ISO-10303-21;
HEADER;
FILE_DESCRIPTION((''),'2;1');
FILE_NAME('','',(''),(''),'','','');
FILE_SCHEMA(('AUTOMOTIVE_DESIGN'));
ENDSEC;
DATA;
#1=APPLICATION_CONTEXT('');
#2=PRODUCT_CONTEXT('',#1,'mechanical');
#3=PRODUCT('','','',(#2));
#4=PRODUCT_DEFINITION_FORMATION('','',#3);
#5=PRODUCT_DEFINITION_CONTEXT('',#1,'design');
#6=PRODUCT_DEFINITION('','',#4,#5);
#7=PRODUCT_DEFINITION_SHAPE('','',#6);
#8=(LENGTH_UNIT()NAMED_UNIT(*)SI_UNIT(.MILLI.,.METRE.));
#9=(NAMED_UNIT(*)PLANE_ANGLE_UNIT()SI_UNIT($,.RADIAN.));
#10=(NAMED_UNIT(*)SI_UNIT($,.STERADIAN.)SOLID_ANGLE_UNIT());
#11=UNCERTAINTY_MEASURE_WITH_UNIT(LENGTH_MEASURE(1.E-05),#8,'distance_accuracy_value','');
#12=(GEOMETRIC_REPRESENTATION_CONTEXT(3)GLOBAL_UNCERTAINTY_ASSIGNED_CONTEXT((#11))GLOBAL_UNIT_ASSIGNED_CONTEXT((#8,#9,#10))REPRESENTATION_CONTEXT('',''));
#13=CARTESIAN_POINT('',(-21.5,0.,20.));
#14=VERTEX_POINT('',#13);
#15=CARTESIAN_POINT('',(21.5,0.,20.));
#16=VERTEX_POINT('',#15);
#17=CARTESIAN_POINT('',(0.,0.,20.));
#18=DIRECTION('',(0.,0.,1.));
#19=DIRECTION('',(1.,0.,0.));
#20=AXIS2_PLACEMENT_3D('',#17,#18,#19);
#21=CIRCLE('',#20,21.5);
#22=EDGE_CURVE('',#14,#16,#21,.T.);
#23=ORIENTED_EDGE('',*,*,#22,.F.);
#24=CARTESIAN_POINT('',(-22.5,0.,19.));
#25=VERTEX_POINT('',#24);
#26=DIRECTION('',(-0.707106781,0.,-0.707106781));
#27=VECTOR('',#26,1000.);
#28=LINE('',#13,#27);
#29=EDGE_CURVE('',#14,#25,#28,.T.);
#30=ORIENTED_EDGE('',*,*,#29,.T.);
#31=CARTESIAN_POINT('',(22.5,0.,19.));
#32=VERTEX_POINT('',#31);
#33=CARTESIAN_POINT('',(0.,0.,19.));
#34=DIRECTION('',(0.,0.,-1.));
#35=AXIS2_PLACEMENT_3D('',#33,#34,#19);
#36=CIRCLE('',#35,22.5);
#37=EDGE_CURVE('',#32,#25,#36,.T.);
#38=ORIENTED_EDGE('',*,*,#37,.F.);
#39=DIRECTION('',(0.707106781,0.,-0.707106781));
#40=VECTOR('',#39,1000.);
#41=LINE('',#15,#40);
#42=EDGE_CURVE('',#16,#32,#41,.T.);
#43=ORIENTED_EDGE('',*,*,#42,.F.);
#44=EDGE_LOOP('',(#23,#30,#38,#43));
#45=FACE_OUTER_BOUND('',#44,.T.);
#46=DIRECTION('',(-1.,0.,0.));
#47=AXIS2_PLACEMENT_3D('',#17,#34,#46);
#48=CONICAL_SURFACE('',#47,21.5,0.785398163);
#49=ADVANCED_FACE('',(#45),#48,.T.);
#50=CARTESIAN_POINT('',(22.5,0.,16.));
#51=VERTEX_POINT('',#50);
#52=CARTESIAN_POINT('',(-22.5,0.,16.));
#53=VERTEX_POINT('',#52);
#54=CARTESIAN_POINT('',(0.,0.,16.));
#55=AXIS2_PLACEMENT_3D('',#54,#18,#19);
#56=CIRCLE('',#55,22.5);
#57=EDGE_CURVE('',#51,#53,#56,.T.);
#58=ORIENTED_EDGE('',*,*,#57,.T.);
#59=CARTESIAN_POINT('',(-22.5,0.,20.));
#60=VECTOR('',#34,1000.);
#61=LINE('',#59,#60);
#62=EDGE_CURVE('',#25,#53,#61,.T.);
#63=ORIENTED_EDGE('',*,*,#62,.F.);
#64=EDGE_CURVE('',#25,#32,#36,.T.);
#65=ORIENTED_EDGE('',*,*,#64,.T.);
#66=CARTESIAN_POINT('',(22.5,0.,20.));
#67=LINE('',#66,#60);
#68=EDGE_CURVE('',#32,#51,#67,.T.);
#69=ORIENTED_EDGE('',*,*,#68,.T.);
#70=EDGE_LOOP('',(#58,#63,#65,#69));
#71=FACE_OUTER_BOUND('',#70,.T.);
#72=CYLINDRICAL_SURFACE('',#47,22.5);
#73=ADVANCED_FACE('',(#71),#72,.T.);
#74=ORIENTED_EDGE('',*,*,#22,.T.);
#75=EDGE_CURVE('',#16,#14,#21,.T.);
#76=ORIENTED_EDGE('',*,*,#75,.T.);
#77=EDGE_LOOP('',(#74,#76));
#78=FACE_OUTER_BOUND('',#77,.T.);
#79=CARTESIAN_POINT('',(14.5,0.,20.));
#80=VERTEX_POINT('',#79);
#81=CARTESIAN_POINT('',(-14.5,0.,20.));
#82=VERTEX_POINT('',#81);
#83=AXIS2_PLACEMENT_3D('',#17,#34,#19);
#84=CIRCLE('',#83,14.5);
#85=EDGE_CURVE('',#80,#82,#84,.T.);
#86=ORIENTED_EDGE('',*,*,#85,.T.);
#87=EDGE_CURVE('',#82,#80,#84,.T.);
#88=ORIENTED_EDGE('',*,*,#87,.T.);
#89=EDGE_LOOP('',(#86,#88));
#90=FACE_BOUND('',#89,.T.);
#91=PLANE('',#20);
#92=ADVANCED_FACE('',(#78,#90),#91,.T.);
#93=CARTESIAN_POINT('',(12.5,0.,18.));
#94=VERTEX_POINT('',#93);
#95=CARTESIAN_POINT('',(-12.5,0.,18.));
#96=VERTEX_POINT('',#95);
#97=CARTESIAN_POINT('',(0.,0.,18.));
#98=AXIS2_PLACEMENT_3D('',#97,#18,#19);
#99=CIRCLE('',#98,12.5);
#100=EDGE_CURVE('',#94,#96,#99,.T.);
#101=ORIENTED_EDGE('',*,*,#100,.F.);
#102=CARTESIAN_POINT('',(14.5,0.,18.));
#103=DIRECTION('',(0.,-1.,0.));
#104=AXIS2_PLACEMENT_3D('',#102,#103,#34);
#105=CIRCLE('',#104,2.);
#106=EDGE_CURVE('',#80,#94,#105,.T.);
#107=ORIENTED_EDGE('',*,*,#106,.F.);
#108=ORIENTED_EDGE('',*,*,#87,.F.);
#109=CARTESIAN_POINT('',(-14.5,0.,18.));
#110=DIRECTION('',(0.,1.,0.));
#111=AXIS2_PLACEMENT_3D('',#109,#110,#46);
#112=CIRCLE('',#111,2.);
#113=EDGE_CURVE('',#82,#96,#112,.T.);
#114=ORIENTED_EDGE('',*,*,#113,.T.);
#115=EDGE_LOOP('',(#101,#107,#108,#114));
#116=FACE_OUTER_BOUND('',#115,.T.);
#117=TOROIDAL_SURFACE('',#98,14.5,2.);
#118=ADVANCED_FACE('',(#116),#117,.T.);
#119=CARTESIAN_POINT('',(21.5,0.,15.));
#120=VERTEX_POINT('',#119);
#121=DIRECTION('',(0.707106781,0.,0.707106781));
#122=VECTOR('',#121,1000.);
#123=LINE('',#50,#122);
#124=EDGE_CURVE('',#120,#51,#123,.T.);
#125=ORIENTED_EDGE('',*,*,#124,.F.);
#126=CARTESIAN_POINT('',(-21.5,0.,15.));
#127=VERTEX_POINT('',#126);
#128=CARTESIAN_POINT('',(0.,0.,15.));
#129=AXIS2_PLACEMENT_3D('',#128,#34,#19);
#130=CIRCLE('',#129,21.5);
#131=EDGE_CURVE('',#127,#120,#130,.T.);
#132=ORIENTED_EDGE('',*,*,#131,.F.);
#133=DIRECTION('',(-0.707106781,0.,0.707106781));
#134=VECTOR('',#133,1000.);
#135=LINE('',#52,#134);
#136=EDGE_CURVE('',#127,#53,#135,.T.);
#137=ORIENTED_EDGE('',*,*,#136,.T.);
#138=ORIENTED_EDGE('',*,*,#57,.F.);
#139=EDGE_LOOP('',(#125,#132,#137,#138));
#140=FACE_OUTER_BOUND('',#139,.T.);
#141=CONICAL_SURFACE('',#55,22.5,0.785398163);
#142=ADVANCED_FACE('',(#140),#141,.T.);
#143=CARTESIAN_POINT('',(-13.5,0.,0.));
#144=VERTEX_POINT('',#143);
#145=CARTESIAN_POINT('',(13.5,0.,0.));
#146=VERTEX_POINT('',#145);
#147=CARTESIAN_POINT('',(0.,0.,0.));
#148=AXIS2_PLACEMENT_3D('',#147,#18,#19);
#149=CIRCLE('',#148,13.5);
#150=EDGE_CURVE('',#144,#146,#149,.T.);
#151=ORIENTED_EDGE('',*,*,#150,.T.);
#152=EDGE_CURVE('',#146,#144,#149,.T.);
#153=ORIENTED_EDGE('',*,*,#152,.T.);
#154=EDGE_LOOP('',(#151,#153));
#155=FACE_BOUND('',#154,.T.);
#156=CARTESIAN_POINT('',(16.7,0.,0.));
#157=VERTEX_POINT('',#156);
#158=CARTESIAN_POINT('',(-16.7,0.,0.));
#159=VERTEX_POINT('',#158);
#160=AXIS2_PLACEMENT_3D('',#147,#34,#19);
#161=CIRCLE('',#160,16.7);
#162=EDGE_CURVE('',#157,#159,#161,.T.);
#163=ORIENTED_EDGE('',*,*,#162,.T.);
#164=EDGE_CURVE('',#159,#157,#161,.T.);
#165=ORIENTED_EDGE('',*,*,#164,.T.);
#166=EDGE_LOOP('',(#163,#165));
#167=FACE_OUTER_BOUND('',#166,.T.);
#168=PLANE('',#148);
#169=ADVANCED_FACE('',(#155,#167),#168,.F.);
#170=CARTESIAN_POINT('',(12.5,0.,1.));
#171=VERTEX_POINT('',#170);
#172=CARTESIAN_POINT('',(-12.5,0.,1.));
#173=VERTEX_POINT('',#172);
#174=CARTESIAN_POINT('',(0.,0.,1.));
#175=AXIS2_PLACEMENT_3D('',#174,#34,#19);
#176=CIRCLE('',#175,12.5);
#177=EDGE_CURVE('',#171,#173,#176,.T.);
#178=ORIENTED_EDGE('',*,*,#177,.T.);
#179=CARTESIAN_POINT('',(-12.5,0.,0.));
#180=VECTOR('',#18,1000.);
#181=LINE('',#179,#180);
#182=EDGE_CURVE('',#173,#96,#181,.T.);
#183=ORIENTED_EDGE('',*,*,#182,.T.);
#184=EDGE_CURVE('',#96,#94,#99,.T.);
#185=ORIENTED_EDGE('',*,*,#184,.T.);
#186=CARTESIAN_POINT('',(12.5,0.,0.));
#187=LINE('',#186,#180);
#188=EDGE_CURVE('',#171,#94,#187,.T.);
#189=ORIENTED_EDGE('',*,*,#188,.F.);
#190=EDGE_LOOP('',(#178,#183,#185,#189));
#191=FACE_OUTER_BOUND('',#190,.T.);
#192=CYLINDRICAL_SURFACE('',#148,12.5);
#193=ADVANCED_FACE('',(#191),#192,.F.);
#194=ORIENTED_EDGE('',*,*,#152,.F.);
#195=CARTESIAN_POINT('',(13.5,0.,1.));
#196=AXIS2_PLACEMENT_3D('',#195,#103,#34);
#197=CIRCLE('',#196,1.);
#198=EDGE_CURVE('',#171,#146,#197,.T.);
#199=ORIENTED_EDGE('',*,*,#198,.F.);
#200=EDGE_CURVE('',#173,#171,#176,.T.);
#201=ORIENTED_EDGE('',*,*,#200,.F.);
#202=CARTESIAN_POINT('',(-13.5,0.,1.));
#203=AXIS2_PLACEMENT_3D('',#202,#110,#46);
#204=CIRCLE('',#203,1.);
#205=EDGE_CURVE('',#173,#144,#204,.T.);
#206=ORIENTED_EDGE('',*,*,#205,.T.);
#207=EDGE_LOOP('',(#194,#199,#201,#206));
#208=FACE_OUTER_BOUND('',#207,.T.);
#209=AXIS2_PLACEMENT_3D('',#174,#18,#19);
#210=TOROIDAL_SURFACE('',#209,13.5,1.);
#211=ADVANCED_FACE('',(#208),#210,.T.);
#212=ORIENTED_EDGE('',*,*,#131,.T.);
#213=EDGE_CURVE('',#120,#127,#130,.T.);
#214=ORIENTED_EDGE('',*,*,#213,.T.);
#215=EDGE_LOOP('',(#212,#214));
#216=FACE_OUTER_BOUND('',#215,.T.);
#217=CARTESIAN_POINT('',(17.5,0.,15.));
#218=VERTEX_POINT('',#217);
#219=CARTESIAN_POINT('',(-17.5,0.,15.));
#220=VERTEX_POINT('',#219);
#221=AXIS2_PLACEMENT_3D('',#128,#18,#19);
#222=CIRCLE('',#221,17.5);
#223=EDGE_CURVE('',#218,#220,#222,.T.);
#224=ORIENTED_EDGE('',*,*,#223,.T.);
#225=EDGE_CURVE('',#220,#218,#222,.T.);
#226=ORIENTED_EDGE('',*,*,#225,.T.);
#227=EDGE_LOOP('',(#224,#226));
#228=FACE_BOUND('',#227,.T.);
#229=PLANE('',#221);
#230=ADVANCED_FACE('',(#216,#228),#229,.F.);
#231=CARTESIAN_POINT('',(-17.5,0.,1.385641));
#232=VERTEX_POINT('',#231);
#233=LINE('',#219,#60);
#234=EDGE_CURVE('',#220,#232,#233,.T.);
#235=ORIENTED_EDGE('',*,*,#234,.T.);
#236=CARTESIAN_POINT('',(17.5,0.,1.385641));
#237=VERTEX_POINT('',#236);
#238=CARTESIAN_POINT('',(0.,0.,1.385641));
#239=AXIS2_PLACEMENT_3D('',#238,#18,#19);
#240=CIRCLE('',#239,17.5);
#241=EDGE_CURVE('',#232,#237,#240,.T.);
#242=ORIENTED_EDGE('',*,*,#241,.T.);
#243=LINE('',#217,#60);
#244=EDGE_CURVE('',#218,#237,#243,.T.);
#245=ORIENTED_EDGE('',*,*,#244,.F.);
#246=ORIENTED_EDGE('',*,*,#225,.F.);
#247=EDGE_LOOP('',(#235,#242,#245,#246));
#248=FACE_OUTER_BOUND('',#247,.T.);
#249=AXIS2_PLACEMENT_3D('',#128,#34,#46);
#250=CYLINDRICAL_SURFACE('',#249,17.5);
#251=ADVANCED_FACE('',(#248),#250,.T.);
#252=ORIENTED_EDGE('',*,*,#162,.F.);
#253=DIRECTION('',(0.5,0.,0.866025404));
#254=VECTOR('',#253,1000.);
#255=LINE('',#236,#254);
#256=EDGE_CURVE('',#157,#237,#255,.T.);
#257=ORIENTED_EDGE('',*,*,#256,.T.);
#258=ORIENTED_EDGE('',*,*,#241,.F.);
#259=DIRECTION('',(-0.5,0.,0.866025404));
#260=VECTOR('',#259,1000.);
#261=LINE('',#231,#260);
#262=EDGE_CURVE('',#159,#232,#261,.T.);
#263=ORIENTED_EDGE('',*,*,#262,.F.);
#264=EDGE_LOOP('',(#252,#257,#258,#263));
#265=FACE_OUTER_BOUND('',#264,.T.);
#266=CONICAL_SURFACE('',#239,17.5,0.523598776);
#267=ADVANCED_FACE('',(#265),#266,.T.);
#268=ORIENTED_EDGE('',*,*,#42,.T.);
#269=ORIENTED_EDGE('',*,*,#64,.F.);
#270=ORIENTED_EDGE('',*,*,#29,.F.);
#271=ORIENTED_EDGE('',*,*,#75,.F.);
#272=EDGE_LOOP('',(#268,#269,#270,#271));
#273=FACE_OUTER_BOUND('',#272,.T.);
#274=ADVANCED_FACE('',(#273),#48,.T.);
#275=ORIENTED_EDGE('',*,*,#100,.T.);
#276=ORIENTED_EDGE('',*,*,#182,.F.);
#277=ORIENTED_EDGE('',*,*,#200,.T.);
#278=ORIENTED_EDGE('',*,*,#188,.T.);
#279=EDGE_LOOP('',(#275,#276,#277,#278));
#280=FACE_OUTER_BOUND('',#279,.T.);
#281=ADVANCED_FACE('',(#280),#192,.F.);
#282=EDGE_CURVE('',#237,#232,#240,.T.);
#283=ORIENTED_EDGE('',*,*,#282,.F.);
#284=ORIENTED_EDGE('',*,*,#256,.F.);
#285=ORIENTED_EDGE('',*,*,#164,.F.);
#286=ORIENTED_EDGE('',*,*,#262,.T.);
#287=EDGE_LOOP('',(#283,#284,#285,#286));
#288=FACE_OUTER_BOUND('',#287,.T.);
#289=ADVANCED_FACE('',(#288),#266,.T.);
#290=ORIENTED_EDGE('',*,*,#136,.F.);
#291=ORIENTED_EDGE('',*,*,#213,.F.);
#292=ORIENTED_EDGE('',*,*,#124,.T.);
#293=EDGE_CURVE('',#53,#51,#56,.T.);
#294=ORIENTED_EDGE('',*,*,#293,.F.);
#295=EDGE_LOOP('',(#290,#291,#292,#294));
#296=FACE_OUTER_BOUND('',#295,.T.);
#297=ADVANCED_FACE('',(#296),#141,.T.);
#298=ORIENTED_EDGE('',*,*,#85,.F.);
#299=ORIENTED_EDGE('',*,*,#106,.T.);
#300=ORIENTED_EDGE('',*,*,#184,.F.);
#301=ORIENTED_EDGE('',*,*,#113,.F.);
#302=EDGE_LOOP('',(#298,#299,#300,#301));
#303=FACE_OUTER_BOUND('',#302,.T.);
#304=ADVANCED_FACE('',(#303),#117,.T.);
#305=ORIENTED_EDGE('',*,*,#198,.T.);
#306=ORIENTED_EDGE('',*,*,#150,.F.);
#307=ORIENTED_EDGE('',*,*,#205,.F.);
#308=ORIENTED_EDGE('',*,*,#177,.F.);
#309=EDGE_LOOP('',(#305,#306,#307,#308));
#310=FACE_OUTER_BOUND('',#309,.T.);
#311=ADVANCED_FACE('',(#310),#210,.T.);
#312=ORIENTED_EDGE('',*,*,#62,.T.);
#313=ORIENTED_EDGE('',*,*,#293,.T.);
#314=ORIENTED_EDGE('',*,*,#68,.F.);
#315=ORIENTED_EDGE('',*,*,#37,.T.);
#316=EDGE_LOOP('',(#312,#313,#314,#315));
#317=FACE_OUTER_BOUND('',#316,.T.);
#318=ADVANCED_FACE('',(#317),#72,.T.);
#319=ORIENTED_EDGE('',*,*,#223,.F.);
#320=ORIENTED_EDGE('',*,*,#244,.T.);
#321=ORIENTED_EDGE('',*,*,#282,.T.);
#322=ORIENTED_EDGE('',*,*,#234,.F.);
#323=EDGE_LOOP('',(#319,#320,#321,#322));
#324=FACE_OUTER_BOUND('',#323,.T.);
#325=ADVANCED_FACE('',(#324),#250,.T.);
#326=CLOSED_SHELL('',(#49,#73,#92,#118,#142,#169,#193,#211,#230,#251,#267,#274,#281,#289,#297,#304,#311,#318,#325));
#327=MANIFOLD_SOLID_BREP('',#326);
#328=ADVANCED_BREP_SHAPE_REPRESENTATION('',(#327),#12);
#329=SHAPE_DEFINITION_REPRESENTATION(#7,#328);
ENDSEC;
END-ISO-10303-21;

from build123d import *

# Parameters (mm, degrees)
BODY_PROFILE_35_R             = 17.5
BODY_35_DEPTH                 = 15
FLANGE_PROFILE_45_R           = 22.5
FLANGE_45_DEPTH               = 5
BODY_END_CHAMFER_0_8X60_SIZE  = 0.8
BODY_END_CHAMFER_0_8X60_SIZE2 = 1.385640646
BORE_PROFILE_25_R             = 12.5
BORE_25_DEPTH                 = 38.583240946
FLANGE_BORE_FILLET_R2_R       = 2
FLANGE_EDGE_CHAMFER_1X45_SIZE = 1
BODY_BORE_FILLET_R1_R         = 1


with BuildPart() as part:
    # Body Profile Ø35 → Body Ø35 (new body)
    with BuildSketch(Plane.XY):
        Circle(BODY_PROFILE_35_R)
    extrude(amount=BODY_35_DEPTH)

    # Flange Profile Ø45 → Flange Ø45 (add)
    with BuildSketch(Plane.XY.offset(15)):
        Circle(FLANGE_PROFILE_45_R)
    extrude(amount=FLANGE_45_DEPTH)

    # Body End Chamfer 0.8x60°
    body_end_chamfer_0_8x60_edges = [part.edges().sort_by_distance(p)[0] for p in [
        (-17.5, 0, 0),
    ]]
    body_end_chamfer_0_8x60_side = [part.faces().sort_by_distance(p)[0] for p in [
        (0, 0, 0),
    ]]
    chamfer(body_end_chamfer_0_8x60_edges, length=BODY_END_CHAMFER_0_8X60_SIZE, length2=BODY_END_CHAMFER_0_8X60_SIZE2, reference=body_end_chamfer_0_8x60_side[0])

    # Bore Profile Ø25 → Bore Ø25 (cut, through all)
    with BuildSketch(Plane.XY.offset(20)):
        Circle(BORE_PROFILE_25_R)
    extrude(amount=-BORE_25_DEPTH, mode=Mode.SUBTRACT)

    # Flange Bore Fillet R2
    flange_bore_fillet_r2_edges = [part.edges().sort_by_distance(p)[0] for p in [
        (-12.5, 0, 20),
    ]]
    fillet(flange_bore_fillet_r2_edges, radius=FLANGE_BORE_FILLET_R2_R)

    # Flange Edge Chamfer 1x45°
    flange_edge_chamfer_1x45_edges = [part.edges().sort_by_distance(p)[0] for p in [
        (-22.5, 0, 15),
        (-22.5, 0, 20),
    ]]
    chamfer(flange_edge_chamfer_1x45_edges, length=FLANGE_EDGE_CHAMFER_1X45_SIZE)

    # Body Bore Fillet R1
    body_bore_fillet_r1_edges = [part.edges().sort_by_distance(p)[0] for p in [
        (-12.5, 0, 0),
    ]]
    fillet(body_bore_fillet_r1_edges, radius=BODY_BORE_FILLET_R1_R)


solid = part.part
